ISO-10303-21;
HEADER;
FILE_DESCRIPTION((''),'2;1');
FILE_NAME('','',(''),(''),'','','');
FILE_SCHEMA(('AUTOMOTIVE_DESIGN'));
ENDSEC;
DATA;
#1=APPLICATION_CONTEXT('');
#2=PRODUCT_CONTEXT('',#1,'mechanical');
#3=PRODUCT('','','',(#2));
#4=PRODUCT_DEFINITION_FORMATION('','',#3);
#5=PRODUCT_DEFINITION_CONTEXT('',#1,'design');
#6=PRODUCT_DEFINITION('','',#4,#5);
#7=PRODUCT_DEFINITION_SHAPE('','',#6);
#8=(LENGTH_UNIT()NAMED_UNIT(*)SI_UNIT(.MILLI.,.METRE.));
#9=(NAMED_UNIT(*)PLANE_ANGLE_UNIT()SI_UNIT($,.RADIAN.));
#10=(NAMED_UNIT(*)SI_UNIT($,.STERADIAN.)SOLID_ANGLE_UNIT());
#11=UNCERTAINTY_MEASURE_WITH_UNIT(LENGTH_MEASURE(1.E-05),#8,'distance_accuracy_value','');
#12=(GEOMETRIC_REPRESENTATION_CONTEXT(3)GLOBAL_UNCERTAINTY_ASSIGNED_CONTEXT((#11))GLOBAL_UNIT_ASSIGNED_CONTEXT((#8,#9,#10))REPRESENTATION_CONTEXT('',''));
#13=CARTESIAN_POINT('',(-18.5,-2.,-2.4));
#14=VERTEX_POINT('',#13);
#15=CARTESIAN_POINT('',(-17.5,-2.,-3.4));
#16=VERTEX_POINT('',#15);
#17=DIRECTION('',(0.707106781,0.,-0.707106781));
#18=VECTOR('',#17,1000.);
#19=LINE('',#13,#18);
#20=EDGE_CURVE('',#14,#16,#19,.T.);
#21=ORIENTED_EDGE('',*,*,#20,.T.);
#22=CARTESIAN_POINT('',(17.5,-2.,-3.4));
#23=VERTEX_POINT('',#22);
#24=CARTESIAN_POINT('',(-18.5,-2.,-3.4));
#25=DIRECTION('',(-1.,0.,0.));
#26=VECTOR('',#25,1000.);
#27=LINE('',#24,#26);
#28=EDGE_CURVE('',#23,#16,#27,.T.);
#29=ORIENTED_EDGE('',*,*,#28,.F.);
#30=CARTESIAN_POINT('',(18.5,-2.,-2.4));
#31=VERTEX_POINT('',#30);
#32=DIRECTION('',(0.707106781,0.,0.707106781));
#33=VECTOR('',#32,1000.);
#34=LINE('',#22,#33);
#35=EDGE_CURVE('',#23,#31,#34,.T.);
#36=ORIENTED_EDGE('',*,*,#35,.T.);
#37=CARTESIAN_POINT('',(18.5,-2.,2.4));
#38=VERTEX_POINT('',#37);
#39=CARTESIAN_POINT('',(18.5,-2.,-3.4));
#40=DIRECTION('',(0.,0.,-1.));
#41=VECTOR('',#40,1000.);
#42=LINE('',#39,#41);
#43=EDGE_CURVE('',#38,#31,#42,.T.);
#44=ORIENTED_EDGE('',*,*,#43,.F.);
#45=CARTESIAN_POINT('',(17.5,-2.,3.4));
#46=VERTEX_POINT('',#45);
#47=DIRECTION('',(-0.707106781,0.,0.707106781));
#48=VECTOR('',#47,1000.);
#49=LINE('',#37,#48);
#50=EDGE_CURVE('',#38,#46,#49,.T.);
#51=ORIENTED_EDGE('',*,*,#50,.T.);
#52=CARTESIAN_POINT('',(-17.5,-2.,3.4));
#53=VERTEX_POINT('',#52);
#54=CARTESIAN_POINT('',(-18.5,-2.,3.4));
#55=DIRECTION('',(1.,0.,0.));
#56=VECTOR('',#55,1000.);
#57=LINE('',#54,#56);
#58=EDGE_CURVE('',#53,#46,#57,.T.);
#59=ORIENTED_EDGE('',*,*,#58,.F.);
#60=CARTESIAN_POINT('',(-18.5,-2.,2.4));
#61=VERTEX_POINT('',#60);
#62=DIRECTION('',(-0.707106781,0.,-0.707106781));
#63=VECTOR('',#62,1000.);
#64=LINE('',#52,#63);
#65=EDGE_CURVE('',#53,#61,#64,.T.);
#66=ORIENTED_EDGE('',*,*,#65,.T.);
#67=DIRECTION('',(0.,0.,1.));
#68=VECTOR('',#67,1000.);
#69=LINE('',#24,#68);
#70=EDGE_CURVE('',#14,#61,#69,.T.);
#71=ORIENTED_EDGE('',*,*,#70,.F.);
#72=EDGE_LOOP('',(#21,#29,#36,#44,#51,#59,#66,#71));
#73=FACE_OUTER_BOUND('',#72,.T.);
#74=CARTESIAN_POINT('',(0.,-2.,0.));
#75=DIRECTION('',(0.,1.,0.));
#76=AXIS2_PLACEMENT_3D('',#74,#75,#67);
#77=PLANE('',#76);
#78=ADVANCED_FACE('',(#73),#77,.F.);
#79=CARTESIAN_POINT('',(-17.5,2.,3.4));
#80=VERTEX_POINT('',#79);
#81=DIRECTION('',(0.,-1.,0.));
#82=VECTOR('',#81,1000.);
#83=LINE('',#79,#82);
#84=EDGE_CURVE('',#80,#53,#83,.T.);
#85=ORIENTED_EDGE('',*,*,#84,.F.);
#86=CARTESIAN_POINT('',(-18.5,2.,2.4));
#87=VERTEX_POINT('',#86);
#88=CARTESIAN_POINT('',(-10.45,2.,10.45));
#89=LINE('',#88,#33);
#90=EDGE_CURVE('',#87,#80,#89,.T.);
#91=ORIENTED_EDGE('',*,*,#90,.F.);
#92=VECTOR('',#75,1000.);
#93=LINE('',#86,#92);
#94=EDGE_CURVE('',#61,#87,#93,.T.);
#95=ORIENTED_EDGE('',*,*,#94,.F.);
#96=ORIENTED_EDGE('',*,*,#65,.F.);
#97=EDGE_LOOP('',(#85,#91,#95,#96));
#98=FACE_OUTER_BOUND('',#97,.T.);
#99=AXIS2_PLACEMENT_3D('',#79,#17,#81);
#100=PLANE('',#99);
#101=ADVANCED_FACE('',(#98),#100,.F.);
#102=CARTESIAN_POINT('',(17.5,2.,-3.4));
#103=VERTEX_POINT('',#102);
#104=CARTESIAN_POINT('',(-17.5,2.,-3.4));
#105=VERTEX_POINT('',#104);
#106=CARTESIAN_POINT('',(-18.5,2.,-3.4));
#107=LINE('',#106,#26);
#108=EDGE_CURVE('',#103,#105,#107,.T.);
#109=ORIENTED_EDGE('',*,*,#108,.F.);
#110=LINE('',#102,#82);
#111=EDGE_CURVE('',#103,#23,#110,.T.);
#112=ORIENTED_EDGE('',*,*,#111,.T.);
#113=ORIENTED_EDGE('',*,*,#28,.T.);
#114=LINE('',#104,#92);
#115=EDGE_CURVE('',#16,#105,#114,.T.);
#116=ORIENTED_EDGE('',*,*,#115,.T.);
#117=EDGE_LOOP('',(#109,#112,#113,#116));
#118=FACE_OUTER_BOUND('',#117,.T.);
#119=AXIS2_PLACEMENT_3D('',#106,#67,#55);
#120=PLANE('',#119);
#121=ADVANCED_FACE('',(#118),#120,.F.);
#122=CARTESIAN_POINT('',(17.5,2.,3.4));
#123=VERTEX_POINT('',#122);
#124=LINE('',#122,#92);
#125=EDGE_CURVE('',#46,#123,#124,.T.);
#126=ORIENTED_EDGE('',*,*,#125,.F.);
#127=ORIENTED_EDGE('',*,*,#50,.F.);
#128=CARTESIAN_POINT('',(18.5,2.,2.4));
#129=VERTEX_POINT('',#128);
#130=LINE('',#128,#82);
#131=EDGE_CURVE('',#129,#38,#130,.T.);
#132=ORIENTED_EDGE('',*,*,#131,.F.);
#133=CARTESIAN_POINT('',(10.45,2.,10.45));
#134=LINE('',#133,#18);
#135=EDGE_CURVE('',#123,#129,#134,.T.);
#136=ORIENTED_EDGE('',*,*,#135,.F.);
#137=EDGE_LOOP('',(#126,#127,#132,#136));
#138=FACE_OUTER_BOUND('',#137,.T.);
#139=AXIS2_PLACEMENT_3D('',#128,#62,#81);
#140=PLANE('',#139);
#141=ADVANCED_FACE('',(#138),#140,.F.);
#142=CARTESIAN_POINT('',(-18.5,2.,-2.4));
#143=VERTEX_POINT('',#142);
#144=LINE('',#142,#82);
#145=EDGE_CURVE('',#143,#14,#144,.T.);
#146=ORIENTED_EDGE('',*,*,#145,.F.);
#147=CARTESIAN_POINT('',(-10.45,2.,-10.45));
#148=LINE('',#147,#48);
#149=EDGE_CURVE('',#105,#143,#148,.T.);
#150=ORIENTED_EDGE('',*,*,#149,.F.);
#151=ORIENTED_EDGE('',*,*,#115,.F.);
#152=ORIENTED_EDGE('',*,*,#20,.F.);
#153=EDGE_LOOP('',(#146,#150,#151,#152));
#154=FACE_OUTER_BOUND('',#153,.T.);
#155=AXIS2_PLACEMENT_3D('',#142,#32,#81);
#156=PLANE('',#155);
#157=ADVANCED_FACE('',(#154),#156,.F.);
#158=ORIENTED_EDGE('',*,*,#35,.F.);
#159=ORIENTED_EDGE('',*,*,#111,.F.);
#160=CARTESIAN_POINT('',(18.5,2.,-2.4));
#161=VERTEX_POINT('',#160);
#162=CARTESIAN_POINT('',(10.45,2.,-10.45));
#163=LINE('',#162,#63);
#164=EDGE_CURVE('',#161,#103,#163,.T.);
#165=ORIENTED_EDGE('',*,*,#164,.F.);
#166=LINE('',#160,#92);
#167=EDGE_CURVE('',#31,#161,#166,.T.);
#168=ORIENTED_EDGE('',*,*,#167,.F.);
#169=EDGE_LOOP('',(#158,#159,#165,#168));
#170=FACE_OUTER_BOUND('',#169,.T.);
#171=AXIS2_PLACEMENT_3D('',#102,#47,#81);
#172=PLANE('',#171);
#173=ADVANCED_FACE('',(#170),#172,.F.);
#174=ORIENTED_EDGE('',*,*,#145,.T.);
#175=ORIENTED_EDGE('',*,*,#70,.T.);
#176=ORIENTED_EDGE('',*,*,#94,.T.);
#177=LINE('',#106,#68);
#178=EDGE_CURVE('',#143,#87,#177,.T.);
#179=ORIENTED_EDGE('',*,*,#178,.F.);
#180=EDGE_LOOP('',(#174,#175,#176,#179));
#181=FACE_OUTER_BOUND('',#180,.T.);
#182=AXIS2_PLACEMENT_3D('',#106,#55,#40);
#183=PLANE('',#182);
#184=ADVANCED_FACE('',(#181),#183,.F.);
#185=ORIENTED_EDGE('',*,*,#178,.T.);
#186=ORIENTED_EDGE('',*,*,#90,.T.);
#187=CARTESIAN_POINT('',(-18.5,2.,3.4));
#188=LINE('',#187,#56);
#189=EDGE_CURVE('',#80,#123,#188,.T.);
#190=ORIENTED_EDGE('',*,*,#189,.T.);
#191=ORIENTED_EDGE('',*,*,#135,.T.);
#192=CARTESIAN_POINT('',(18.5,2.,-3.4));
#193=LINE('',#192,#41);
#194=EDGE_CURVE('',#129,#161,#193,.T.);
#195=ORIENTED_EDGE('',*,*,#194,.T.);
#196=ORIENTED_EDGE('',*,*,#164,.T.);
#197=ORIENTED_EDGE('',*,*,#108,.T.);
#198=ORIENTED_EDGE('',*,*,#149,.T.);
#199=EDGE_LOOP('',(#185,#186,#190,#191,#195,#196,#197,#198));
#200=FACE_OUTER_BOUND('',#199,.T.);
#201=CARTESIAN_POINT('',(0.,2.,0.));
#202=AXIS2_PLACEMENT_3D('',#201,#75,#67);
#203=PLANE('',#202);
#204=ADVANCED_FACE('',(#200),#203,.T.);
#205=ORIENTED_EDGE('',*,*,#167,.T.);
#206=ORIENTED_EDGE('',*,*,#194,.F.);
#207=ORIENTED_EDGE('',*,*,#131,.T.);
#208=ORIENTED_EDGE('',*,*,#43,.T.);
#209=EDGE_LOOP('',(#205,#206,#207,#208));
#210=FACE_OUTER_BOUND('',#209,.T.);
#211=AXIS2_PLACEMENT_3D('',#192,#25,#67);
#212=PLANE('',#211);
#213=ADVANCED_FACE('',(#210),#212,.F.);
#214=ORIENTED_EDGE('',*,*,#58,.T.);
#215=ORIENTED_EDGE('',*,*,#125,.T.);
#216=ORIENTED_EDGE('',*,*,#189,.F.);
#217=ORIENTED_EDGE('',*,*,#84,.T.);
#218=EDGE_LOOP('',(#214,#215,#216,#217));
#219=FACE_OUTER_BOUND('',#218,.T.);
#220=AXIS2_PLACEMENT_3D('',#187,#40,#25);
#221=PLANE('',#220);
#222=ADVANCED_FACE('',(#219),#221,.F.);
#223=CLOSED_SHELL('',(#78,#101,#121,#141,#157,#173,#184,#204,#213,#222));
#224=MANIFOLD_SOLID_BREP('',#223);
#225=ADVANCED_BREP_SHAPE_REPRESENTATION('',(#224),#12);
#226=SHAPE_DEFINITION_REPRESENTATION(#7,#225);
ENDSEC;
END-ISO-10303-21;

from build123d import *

# Parameters (mm, degrees)
SKETCH1_W           = 37
SKETCH1_H           = 6.8
BOSS_EXTRUDE1_DEPTH = 2
CHAMFER1_SIZE       = 1


with BuildPart() as part:
    # Sketch1 → Boss-Extrude1 (new, symmetric)
    with BuildSketch(Plane(origin=(0, 0, 0), x_dir=(1, 0, 0), z_dir=(0, 1, 0))):
        Rectangle(SKETCH1_W, SKETCH1_H)
    extrude(amount=BOSS_EXTRUDE1_DEPTH, both=True)

    # Chamfer1
    chamfer1_edges = [part.edges().sort_by_distance(p)[0] for p in [
        (18.5, 0, 3.4),
        (-18.5, 0, 3.4),
        (-18.5, 0, -3.4),
        (18.5, 0, -3.4),
    ]]
    chamfer(chamfer1_edges, length=CHAMFER1_SIZE)


solid = part.part
